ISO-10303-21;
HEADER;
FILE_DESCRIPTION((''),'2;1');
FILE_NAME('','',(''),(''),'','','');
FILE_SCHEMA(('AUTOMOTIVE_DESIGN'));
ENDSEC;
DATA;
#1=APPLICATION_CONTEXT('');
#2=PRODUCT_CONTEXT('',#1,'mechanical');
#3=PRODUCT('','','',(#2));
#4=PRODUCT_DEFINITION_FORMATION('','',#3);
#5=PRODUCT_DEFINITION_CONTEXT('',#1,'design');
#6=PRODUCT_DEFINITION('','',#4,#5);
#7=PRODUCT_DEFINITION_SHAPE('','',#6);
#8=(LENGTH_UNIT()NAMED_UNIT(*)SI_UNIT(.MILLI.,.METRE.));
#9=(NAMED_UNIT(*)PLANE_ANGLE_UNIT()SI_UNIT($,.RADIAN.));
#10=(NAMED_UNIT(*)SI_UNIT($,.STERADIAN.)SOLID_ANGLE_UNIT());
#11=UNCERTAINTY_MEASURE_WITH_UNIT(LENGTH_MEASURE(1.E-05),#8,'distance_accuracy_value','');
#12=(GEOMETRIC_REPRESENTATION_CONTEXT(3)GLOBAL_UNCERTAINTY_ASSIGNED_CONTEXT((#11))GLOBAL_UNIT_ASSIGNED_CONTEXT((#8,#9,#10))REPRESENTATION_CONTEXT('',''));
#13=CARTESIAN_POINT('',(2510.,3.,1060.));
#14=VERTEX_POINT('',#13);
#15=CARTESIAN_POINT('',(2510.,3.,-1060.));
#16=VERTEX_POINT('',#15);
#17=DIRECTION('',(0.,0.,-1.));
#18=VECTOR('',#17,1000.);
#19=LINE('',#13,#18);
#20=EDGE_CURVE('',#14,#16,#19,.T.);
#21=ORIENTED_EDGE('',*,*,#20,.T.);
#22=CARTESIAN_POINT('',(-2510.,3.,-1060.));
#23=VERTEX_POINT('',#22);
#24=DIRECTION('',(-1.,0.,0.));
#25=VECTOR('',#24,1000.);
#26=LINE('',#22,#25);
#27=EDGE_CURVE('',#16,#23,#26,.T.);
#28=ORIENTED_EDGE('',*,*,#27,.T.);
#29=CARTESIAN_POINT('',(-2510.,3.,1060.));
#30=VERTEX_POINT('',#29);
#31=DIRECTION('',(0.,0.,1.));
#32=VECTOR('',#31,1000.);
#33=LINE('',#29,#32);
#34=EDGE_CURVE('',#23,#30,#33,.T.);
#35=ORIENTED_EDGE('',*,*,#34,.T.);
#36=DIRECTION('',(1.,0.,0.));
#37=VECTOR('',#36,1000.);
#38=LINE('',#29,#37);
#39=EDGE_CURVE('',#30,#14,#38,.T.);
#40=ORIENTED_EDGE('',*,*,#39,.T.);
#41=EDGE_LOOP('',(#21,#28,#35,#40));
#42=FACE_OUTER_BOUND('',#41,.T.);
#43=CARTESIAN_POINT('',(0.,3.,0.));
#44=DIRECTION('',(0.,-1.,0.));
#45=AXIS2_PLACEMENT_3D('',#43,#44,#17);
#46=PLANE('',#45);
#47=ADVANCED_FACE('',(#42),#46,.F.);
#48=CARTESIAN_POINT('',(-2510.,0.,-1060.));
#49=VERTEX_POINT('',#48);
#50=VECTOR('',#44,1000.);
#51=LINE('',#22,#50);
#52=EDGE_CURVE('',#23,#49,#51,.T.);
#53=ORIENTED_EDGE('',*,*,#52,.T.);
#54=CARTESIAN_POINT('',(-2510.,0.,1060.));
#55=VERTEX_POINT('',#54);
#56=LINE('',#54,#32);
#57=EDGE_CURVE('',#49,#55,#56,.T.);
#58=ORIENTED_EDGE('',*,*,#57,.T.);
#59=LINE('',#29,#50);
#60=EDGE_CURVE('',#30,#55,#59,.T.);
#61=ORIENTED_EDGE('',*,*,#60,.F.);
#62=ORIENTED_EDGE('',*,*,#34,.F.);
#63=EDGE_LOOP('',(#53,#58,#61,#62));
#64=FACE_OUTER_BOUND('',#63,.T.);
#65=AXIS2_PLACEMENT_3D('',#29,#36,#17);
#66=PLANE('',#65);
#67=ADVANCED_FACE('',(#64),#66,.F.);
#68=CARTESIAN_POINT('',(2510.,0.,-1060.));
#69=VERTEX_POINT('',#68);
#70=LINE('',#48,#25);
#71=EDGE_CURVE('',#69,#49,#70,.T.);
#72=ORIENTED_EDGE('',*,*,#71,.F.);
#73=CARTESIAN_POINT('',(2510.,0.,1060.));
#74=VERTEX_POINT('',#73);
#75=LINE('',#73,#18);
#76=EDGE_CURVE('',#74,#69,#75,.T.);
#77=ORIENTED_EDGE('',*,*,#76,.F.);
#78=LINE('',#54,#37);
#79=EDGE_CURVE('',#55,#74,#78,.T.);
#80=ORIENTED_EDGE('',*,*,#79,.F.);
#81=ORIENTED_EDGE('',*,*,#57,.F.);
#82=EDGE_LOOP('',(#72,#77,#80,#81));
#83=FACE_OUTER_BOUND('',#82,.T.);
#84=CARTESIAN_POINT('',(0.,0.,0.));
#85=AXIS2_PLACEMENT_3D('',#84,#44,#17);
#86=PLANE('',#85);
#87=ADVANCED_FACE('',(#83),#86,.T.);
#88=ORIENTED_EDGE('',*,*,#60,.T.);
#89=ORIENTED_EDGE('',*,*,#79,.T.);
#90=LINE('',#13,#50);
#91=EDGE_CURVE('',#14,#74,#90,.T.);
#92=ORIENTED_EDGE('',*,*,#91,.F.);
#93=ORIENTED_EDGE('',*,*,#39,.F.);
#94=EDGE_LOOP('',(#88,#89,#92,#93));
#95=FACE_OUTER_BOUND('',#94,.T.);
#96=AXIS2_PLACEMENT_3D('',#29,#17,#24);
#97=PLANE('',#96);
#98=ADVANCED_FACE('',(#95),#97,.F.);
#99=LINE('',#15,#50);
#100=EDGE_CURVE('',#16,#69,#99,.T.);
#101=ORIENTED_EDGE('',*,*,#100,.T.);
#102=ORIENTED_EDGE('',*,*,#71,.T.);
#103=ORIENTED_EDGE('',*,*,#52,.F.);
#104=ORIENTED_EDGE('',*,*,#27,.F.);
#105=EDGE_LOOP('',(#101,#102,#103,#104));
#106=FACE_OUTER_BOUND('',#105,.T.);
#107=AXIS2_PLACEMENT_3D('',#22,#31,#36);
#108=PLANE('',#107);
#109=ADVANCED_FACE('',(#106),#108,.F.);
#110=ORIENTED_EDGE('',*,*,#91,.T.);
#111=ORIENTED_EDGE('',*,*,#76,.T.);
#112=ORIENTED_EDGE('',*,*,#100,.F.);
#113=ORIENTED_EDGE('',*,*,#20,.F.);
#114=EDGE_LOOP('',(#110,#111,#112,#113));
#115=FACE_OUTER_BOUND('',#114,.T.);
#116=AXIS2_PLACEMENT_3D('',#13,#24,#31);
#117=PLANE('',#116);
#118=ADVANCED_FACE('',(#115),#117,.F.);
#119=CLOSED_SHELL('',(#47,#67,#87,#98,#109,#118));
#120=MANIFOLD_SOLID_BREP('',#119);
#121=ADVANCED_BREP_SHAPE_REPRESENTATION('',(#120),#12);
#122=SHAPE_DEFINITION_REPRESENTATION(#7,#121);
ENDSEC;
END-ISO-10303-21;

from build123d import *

# Parameters (mm, degrees)
SKETCH_1_W           = 5020
SKETCH_1_H           = 2120
BOSS_EXTRUDE_1_DEPTH = 3


with BuildPart() as part:
    # Sketch 1 → Boss-Extrude 1 (new body)
    with BuildSketch(Plane(origin=(0, 0, 0), x_dir=(1, 0, 0), z_dir=(0, 1, 0))):
        Rectangle(SKETCH_1_W, SKETCH_1_H)
    extrude(amount=BOSS_EXTRUDE_1_DEPTH)


solid = part.part
